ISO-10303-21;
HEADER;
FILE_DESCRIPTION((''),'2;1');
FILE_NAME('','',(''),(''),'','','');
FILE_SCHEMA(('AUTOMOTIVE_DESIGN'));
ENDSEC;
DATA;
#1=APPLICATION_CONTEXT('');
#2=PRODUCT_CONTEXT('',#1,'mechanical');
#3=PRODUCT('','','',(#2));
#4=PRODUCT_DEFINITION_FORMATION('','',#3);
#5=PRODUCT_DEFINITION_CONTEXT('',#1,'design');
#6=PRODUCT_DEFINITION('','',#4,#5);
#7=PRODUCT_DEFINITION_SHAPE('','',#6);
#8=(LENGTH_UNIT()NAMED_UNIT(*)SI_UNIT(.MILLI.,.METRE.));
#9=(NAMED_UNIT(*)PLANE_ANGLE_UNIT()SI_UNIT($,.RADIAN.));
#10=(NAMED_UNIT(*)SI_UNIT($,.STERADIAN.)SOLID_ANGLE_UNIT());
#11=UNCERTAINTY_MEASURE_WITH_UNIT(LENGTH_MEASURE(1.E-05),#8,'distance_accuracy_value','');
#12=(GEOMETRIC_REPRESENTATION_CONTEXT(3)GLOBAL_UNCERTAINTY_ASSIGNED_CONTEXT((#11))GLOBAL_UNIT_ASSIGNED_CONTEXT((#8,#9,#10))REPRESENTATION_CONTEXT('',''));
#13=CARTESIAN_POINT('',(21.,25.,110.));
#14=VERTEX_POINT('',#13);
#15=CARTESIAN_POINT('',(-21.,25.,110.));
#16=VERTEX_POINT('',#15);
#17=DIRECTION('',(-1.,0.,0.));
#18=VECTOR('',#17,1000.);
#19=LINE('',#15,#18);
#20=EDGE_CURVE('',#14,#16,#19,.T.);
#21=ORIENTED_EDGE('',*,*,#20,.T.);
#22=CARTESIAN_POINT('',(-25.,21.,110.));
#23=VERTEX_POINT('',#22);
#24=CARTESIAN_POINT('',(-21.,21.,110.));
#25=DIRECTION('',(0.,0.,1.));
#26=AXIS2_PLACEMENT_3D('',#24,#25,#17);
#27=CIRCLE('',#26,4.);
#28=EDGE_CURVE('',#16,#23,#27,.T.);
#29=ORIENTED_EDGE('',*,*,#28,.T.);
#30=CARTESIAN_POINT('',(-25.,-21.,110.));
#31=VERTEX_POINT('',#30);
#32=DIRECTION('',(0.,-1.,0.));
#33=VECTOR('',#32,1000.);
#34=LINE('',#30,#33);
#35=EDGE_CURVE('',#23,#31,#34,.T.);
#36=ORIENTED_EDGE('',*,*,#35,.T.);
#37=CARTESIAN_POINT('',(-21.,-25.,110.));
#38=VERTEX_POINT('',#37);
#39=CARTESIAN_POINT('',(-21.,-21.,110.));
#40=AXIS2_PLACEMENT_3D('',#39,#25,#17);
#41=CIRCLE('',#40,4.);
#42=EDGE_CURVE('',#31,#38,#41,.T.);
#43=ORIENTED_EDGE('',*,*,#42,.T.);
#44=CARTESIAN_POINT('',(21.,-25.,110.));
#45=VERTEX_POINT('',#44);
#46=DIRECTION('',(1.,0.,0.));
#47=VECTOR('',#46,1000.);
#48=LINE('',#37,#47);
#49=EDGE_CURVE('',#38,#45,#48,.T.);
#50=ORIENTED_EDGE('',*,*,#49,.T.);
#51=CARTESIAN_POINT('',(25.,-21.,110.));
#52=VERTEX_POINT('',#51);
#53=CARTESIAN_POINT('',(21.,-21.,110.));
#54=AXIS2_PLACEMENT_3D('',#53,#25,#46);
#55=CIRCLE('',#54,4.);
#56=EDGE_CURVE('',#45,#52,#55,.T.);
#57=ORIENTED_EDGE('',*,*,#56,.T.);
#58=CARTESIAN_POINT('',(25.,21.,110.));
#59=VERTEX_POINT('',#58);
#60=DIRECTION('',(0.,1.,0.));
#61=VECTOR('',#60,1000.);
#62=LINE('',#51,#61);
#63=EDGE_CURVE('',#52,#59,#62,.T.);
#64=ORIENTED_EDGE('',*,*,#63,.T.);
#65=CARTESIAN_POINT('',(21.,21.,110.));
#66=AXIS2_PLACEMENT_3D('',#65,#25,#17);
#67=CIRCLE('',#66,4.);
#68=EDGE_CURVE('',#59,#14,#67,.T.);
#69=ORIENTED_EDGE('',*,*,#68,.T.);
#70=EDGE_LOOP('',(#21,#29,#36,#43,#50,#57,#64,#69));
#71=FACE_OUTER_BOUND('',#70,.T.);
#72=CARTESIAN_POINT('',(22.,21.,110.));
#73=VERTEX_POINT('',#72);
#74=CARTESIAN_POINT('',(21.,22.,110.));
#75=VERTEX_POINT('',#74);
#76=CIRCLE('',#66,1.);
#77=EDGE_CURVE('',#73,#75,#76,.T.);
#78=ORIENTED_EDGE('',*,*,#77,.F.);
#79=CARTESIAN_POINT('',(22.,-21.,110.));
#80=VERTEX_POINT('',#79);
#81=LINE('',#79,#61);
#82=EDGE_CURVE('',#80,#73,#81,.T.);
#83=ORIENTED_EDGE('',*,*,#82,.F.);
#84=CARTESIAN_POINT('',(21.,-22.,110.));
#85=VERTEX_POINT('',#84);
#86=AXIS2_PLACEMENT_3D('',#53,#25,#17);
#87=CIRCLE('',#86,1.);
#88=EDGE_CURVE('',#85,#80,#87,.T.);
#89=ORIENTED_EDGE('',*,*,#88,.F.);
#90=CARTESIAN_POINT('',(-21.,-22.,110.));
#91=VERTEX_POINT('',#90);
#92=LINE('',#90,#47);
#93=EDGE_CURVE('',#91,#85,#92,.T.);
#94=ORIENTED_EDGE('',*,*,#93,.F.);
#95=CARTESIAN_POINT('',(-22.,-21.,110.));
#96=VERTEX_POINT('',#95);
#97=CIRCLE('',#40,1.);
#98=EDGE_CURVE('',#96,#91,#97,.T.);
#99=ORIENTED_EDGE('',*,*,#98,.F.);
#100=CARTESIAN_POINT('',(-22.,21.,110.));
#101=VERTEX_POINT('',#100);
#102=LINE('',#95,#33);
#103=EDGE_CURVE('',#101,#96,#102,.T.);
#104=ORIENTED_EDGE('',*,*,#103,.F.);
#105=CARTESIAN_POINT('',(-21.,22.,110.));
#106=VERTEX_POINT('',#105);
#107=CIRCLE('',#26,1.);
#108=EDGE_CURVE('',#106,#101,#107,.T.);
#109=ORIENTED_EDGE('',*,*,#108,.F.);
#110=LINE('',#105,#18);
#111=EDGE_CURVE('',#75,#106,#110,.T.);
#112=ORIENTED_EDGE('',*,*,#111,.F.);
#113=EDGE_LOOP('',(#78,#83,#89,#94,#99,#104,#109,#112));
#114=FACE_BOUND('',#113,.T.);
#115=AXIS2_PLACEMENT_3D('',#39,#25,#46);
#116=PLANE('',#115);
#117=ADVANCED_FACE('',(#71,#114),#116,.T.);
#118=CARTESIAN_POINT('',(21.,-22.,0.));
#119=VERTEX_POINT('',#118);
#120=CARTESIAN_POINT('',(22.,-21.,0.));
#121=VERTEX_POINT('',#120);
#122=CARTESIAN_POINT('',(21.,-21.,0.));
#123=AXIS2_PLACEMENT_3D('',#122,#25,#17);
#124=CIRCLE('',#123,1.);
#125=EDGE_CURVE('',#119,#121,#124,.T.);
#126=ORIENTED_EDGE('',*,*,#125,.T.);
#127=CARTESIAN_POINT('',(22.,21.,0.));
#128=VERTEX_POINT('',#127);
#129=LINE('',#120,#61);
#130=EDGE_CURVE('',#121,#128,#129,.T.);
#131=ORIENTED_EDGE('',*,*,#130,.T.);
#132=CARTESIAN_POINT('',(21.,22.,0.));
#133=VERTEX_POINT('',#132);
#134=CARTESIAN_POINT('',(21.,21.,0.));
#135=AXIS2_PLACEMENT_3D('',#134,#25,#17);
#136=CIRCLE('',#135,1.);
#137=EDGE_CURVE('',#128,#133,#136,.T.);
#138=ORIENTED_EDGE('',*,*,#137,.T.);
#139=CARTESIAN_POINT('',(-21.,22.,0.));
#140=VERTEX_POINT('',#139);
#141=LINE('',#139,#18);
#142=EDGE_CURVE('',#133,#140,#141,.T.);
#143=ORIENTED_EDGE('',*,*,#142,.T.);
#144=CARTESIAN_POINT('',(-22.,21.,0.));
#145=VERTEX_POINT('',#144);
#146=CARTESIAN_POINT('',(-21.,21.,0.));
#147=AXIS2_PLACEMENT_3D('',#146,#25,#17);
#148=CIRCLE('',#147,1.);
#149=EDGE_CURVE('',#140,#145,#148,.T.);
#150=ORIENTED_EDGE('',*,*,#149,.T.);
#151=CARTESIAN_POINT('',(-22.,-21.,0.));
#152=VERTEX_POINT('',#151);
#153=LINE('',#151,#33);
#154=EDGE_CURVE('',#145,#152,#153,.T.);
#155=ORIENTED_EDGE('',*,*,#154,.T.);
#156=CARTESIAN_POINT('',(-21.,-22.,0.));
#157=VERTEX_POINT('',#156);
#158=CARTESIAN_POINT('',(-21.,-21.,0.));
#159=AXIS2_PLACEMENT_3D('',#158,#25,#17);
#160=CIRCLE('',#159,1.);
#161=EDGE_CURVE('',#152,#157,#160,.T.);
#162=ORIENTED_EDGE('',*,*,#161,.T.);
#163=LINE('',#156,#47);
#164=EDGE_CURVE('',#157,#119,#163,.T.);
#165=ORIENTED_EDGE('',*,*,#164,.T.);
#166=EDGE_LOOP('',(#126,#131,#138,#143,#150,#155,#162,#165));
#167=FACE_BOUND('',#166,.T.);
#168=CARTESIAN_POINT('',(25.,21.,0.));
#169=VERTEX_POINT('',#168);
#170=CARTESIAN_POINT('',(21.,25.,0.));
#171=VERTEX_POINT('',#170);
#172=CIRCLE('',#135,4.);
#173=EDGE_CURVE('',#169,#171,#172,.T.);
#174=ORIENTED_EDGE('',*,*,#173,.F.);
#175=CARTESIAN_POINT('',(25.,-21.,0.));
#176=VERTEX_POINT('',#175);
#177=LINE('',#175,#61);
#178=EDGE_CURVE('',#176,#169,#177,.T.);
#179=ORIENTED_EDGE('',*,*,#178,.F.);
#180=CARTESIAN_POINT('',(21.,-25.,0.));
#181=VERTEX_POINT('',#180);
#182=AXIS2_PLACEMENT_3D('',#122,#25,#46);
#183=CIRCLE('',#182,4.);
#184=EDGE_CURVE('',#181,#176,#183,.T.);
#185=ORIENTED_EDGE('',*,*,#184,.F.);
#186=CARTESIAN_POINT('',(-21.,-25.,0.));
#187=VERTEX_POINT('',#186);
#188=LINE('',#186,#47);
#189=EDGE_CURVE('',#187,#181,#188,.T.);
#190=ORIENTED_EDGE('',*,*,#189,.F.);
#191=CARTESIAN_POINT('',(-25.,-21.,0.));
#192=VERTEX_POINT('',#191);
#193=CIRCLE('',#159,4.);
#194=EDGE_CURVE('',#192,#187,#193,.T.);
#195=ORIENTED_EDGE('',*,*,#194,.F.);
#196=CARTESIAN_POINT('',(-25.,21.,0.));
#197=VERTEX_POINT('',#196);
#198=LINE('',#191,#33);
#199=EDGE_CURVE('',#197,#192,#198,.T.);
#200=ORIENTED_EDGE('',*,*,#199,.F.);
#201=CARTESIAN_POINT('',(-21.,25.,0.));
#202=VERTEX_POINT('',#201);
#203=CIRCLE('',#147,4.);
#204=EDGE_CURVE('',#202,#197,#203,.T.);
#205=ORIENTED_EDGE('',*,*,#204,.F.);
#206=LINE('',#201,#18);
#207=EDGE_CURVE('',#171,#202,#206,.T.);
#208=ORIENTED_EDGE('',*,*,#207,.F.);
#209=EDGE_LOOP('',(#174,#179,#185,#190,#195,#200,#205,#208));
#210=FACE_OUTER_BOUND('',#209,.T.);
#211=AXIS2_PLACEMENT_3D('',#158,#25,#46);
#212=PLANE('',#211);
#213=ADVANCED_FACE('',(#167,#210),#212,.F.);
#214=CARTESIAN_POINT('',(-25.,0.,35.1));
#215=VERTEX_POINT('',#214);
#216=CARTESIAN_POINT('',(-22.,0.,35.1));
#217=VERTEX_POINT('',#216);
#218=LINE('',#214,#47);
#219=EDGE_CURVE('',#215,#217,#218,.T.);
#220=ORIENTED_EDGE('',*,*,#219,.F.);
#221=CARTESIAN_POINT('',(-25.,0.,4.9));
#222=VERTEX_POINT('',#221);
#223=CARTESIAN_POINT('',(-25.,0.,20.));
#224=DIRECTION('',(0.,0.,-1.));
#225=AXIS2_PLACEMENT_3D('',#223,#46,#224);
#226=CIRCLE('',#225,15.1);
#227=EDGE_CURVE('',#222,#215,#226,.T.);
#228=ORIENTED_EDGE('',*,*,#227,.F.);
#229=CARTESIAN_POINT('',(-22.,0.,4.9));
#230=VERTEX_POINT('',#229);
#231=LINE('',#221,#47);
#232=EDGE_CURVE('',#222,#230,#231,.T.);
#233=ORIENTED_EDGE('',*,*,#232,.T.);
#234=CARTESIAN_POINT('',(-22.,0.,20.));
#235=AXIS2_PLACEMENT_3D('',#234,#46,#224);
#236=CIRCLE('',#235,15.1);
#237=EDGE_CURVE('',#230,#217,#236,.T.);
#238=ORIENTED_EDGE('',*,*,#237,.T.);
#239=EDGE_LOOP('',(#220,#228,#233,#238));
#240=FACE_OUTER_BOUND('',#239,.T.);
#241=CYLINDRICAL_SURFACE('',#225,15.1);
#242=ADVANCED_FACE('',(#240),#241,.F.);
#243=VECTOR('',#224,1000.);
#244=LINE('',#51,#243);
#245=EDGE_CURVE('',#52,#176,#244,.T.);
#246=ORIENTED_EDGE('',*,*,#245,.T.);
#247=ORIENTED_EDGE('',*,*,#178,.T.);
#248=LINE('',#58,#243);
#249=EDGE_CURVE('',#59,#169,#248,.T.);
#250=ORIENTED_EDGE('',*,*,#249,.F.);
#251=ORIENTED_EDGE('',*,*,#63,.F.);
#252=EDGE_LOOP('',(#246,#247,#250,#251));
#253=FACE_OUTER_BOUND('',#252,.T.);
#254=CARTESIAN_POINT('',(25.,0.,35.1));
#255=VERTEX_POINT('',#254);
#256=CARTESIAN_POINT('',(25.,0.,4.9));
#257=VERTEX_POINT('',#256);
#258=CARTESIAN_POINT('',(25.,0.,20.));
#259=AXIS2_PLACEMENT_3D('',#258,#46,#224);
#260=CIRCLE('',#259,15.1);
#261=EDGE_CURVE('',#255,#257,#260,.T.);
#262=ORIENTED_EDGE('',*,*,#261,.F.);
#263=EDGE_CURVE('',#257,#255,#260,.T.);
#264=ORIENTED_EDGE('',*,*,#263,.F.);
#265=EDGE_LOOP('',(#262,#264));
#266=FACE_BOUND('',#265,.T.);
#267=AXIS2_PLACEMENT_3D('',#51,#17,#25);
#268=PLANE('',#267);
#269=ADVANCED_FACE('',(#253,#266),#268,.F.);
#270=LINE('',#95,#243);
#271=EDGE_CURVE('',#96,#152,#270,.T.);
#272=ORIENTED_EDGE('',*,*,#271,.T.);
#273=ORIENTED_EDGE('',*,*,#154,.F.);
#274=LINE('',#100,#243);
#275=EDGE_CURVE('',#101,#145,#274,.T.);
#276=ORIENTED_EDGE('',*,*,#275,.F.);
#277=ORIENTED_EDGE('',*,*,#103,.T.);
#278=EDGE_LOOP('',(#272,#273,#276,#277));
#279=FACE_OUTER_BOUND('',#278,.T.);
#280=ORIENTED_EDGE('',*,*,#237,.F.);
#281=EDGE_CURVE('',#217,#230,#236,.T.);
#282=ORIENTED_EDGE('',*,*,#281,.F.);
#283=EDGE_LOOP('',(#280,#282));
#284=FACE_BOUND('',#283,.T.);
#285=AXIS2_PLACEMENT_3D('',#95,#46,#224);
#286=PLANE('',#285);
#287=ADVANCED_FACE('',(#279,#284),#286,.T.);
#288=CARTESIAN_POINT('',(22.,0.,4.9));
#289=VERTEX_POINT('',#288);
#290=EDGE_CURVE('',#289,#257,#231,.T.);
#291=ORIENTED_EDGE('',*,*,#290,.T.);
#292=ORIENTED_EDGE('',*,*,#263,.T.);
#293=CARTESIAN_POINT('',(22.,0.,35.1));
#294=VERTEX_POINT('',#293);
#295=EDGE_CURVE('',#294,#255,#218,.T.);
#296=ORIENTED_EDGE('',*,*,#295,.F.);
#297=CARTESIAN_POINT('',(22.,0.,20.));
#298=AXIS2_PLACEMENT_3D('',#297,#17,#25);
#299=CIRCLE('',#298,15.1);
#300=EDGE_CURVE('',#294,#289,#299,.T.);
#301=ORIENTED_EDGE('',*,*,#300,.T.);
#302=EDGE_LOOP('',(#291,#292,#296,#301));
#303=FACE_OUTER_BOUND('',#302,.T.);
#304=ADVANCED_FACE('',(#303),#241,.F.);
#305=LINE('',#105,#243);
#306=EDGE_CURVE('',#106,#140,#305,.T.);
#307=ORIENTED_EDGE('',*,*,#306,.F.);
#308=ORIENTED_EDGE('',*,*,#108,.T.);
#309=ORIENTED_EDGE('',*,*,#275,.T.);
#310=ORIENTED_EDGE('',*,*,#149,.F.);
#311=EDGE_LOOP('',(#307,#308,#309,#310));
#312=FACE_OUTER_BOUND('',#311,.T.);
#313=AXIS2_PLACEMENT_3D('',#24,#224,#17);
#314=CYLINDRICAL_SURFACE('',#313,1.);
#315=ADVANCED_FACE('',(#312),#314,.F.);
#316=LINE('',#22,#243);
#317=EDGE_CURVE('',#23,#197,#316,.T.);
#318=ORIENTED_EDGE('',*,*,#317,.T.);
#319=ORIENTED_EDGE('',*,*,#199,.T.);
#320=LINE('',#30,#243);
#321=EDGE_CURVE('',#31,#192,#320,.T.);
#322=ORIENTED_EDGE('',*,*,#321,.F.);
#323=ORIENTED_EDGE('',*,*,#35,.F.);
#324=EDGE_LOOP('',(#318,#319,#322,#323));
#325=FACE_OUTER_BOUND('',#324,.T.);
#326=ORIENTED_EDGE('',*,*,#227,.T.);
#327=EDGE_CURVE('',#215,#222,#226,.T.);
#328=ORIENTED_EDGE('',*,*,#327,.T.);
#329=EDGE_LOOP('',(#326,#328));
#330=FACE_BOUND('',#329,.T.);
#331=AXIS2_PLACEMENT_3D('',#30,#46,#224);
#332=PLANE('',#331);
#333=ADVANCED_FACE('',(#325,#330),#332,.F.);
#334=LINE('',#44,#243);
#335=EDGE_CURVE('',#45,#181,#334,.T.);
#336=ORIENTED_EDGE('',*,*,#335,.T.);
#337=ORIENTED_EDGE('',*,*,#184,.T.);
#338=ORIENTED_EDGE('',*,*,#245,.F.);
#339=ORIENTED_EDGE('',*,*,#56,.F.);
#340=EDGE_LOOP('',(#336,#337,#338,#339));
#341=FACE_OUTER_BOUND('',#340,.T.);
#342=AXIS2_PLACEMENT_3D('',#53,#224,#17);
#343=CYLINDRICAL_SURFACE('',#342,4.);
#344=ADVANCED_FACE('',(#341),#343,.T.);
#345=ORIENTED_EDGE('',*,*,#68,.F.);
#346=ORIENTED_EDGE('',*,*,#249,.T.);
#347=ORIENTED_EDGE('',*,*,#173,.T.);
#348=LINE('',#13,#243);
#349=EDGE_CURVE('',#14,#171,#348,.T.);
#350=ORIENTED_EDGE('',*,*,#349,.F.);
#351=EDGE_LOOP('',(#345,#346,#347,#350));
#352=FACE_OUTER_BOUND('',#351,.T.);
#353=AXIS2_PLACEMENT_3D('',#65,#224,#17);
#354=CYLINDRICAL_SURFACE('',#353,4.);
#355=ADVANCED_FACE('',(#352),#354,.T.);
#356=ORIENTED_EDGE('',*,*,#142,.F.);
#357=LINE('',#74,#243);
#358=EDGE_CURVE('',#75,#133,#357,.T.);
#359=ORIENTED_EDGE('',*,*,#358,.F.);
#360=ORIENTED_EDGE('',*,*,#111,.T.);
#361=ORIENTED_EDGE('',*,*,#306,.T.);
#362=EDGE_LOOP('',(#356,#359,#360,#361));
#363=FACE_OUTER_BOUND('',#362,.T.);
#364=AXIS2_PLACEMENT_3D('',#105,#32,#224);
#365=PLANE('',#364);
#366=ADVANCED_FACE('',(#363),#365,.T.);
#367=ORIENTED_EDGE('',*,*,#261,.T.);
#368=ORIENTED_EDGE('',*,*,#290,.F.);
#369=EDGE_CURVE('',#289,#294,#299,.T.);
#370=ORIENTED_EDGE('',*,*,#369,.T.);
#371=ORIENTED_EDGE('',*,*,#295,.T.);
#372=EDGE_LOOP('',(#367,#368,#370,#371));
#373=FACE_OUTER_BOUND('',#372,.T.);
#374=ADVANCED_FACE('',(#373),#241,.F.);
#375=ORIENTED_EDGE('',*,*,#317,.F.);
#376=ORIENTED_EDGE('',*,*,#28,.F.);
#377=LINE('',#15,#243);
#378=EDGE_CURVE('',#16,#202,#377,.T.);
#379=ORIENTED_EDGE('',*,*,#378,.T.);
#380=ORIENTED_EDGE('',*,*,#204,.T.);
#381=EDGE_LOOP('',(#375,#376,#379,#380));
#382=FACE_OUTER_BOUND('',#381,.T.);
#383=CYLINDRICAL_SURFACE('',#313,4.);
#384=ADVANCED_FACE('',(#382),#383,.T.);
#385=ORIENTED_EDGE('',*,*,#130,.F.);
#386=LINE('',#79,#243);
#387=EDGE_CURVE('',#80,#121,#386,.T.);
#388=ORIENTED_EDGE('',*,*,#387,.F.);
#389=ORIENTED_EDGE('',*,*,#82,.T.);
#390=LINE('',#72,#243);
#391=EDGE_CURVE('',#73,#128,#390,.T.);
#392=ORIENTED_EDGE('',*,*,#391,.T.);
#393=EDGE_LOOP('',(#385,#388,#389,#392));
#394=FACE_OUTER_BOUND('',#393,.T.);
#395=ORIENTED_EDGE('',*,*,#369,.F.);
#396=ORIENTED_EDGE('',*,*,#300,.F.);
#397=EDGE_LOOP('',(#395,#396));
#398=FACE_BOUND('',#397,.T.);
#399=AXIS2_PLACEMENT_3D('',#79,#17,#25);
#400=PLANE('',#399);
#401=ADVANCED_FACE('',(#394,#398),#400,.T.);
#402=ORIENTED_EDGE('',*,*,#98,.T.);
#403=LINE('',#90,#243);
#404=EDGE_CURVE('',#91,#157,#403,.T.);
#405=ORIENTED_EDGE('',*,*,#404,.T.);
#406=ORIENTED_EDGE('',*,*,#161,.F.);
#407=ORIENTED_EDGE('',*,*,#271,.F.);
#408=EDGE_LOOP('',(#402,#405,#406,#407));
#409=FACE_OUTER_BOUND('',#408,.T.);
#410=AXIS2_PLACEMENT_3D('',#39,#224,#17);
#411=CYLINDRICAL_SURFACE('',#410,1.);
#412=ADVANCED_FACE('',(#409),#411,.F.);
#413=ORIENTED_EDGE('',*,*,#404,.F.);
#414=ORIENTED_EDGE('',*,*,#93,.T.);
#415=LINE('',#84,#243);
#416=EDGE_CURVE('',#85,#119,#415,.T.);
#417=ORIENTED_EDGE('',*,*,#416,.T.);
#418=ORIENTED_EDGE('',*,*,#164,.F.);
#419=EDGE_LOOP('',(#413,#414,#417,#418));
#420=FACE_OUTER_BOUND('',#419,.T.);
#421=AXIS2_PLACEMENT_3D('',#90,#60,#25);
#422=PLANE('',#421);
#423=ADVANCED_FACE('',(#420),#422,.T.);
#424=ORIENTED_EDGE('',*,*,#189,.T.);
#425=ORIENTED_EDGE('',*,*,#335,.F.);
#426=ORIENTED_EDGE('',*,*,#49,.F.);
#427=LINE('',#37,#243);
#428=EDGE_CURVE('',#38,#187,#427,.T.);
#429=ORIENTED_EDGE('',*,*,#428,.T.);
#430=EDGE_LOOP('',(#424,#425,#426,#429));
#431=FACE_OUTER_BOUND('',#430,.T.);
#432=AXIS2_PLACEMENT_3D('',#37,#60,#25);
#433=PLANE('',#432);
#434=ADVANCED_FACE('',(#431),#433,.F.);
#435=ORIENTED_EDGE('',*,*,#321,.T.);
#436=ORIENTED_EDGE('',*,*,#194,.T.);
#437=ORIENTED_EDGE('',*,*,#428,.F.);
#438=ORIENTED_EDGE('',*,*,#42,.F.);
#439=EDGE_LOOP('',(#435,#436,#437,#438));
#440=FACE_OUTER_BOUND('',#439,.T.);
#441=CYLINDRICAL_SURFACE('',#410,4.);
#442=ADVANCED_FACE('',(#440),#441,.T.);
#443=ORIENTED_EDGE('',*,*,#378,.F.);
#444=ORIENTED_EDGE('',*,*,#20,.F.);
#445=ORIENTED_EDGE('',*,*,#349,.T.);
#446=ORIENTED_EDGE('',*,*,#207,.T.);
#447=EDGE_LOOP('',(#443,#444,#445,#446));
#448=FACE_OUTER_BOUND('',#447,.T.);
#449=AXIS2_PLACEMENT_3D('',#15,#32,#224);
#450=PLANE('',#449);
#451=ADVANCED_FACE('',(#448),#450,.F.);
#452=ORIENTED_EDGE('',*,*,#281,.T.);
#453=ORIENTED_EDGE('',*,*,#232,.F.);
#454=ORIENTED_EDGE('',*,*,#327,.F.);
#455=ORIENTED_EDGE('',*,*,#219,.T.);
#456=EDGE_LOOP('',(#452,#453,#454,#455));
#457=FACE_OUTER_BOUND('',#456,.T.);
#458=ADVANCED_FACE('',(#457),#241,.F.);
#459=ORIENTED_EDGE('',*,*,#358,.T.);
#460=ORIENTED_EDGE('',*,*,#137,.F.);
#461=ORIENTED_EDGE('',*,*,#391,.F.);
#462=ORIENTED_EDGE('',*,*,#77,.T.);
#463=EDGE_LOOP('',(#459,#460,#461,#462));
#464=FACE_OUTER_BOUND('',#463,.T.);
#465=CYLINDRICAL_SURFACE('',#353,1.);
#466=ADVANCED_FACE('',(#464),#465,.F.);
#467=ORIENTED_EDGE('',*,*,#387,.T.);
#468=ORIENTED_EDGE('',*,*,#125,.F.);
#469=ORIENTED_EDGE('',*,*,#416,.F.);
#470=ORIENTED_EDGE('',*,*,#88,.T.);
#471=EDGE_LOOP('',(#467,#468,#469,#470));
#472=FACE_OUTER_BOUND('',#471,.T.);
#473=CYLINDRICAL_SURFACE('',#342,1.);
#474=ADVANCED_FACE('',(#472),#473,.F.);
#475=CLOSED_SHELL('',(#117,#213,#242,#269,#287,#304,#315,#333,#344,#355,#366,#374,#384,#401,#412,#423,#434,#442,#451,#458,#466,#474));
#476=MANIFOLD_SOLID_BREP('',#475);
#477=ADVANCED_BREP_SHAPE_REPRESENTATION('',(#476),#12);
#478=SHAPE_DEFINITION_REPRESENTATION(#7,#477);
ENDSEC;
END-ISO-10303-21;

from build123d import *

# Parameters (mm, degrees)
EXTRUDE_THIN1_DEPTH = 110
SKETCH2_R           = 15.1
CUT_EXTRUDE1_DEPTH  = 124.389626793


with BuildPart() as part:
    # Sketch1 → Extrude-Thin1 (new body)
    with BuildSketch(Plane.XY):
        with BuildLine():
            Line((-25, 21), (-25, -21))
            ThreePointArc((-25, -21), (-23.828427125, -23.828427125), (-21, -25))
            Line((-21, -25), (21, -25))
            ThreePointArc((21, -25), (23.828427125, -23.828427125), (25, -21))
            Line((25, -21), (25, 21))
            ThreePointArc((25, 21), (23.828427125, 23.828427125), (21, 25))
            Line((21, 25), (-21, 25))
            ThreePointArc((-21, 25), (-23.828427125, 23.828427125), (-25, 21))
        make_face()
        with BuildLine():
            Line((-22, 21), (-22, -21))
            ThreePointArc((-22, -21), (-21.707106781, -21.707106781), (-21, -22))
            Line((-21, -22), (21, -22))
            ThreePointArc((21, -22), (21.707106781, -21.707106781), (22, -21))
            Line((22, -21), (22, 21))
            ThreePointArc((22, 21), (21.707106781, 21.707106781), (21, 22))
            Line((21, 22), (-21, 22))
            ThreePointArc((-21, 22), (-21.707106781, 21.707106781), (-22, 21))
        make_face(mode=Mode.SUBTRACT)
    extrude(amount=EXTRUDE_THIN1_DEPTH)

    # Sketch2 → Cut-Extrude1 (cut, through all)
    with BuildSketch(Plane(origin=(25, 0, 0), x_dir=(0, 0, -1), z_dir=(1, 0, 0))):
        with Locations((-20, 0)):
            Circle(SKETCH2_R)
    extrude(amount=-CUT_EXTRUDE1_DEPTH, mode=Mode.SUBTRACT)


solid = part.part
